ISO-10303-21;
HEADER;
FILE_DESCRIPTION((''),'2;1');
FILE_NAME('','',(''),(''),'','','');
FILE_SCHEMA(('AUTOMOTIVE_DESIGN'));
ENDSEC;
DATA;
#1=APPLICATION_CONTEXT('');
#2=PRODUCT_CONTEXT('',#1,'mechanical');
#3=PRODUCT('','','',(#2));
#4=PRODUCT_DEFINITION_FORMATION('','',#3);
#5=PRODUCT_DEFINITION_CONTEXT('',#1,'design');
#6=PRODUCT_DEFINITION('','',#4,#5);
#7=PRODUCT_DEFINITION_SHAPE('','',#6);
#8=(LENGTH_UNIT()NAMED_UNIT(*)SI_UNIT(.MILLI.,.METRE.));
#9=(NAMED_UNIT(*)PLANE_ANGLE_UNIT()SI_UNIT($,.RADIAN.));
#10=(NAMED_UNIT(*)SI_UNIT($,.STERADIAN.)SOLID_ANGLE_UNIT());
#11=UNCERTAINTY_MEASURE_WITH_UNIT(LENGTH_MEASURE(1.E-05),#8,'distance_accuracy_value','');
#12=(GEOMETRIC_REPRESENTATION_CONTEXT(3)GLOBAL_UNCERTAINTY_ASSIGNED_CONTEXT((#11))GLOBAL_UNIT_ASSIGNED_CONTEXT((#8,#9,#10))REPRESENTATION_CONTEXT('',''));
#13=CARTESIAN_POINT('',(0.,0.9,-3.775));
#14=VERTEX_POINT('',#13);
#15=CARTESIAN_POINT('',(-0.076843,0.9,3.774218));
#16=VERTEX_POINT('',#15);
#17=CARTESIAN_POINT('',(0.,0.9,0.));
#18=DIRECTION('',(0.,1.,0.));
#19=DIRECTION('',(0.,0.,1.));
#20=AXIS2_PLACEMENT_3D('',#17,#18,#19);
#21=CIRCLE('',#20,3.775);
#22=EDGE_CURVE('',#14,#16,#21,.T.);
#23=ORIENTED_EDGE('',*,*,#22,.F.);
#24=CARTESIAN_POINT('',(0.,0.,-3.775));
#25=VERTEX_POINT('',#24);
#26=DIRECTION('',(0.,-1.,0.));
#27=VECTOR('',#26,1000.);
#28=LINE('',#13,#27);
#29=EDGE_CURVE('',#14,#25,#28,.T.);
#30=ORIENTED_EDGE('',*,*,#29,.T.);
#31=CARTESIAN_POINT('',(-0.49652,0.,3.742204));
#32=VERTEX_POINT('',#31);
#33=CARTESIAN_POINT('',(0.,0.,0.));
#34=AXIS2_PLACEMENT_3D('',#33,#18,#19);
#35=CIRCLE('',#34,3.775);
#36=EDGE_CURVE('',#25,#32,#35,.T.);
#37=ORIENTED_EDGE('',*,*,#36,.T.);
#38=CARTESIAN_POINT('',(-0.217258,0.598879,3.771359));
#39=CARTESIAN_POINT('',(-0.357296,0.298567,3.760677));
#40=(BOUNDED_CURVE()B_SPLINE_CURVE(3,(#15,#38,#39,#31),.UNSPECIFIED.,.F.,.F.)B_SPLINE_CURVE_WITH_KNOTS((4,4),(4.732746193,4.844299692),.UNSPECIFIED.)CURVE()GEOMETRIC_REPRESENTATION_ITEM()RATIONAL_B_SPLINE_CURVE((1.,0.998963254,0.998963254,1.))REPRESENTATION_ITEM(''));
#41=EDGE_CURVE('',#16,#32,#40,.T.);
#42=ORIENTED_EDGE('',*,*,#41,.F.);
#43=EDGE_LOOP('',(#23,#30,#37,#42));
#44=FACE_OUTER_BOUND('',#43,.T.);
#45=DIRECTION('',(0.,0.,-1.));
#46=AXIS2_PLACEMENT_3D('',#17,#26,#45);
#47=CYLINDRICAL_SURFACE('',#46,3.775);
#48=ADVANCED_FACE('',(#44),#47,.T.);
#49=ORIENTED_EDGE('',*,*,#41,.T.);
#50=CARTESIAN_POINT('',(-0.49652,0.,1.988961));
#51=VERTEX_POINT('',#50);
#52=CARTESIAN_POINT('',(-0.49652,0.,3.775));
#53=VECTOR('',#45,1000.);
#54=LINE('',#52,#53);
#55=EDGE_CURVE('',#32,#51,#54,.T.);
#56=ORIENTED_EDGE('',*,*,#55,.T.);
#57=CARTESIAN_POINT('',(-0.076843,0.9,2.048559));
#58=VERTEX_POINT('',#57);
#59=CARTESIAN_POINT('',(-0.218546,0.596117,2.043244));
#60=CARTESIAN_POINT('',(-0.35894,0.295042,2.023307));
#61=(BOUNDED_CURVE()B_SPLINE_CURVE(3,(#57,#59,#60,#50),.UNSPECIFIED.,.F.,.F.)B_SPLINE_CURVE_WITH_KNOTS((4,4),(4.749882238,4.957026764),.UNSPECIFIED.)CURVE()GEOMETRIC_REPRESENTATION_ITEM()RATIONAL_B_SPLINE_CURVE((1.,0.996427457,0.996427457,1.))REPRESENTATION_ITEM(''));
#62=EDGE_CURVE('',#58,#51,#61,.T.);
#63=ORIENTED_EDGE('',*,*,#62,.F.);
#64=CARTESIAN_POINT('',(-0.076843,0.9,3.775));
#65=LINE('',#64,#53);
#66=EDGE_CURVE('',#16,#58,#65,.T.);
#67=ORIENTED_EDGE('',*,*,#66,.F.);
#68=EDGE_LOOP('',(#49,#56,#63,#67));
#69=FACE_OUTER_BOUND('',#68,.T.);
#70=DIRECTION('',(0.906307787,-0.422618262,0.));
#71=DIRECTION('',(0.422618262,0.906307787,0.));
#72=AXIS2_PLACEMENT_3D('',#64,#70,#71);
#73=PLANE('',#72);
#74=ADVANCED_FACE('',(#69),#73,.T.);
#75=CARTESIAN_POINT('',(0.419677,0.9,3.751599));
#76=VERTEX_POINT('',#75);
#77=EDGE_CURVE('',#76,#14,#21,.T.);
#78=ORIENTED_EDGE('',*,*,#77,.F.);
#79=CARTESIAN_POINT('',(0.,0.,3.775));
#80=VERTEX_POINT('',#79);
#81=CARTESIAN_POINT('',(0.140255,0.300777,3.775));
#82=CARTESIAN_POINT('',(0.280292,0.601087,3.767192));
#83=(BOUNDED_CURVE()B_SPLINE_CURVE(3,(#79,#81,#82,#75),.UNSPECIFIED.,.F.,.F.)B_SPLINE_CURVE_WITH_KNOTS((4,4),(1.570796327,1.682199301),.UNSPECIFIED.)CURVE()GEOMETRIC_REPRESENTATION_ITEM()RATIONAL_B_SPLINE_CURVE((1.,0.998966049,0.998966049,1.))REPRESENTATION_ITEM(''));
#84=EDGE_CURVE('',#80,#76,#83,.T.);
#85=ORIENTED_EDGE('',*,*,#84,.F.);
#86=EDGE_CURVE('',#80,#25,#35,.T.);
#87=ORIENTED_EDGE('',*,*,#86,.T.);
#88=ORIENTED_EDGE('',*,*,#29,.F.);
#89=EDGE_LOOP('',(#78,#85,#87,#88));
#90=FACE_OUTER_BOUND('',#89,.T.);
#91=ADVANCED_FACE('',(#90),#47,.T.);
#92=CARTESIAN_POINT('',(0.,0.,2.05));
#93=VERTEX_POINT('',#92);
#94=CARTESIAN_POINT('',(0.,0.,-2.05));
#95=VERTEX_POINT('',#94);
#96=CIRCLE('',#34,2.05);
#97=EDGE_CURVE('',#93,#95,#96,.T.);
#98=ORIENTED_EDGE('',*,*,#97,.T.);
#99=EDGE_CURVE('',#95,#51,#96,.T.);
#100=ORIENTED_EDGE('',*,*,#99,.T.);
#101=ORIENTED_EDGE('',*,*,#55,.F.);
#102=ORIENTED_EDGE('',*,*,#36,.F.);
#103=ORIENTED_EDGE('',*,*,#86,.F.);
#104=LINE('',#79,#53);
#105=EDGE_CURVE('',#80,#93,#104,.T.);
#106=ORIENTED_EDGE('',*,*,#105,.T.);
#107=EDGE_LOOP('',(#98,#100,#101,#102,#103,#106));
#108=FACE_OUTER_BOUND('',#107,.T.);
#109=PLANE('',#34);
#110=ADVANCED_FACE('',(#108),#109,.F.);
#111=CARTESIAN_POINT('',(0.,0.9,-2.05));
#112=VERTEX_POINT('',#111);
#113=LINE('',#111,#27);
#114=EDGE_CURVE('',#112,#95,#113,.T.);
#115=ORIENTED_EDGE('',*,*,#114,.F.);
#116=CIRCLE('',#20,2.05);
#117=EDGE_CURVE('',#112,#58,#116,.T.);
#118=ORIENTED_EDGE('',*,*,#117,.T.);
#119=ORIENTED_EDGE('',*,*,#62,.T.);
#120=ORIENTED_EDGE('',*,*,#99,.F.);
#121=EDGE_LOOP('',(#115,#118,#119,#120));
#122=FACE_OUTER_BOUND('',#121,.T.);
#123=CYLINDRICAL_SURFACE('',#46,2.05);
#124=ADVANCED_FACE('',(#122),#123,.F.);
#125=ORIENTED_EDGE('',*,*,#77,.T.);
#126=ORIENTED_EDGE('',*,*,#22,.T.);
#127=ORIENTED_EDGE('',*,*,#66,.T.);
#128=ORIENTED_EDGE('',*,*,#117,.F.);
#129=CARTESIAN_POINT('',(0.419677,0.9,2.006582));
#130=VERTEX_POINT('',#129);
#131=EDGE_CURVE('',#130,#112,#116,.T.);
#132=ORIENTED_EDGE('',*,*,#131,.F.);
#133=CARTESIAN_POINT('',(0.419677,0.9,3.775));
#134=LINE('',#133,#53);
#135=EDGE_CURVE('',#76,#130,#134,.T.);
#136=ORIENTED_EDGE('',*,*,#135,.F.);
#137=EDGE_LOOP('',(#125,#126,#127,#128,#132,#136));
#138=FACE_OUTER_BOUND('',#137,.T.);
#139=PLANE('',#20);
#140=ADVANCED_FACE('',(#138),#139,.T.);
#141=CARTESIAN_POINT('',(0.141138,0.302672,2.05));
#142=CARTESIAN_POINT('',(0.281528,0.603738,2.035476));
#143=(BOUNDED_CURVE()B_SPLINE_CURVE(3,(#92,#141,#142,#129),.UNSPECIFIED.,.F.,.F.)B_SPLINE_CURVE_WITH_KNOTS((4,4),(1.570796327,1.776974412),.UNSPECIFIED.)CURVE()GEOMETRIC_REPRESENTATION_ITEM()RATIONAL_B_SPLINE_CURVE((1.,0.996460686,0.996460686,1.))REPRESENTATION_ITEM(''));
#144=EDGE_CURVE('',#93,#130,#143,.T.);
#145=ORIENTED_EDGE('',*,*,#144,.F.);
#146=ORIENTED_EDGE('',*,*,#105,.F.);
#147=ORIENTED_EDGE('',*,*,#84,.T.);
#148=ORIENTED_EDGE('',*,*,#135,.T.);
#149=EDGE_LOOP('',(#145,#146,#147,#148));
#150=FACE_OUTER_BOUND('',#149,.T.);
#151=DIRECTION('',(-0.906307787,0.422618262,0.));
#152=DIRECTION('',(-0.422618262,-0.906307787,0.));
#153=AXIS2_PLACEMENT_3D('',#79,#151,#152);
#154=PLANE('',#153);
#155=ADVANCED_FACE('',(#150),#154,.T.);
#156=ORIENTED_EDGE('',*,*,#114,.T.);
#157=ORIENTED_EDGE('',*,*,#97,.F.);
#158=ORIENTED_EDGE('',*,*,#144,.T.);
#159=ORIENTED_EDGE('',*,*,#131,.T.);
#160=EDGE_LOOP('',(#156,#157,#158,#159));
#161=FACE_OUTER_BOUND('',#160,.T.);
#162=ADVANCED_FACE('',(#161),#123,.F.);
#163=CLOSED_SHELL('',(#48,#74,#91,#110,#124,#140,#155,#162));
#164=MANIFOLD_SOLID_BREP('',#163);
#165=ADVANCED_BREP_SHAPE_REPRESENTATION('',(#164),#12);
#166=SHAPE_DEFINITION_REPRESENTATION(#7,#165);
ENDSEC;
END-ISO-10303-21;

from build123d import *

# Parameters (mm, degrees)
SKETCH_1_R          = 3.775
SKETCH_1_R_2        = 2.05
EXTRUDE_1_DEPTH     = 0.9
CUT_EXTRUDE_1_DEPTH = 6.413986516


with BuildPart() as part:
    # 草图1 → 凸台-拉伸1 (new body)
    with BuildSketch(Plane(origin=(0, 0, 0), x_dir=(1, 0, 0), z_dir=(0, 1, 0))):
        with Locations(Location((0, 0, 0), (0, 0, 270))):
            Circle(SKETCH_1_R)
        with Locations(Location((0, 0, 0), (0, 0, 270))):
            Circle(SKETCH_1_R_2, mode=Mode.SUBTRACT)
    extrude(amount=EXTRUDE_1_DEPTH)

    # 草图2 → 切除-拉伸1 (cut, through all)
    with BuildSketch(Plane.XY):
        Polygon((0, 0), (0.419676892, 0.9), (-0.076843171, 0.9), (-0.496520064, 0), align=None)
    extrude(amount=CUT_EXTRUDE_1_DEPTH, mode=Mode.SUBTRACT)


solid = part.part
